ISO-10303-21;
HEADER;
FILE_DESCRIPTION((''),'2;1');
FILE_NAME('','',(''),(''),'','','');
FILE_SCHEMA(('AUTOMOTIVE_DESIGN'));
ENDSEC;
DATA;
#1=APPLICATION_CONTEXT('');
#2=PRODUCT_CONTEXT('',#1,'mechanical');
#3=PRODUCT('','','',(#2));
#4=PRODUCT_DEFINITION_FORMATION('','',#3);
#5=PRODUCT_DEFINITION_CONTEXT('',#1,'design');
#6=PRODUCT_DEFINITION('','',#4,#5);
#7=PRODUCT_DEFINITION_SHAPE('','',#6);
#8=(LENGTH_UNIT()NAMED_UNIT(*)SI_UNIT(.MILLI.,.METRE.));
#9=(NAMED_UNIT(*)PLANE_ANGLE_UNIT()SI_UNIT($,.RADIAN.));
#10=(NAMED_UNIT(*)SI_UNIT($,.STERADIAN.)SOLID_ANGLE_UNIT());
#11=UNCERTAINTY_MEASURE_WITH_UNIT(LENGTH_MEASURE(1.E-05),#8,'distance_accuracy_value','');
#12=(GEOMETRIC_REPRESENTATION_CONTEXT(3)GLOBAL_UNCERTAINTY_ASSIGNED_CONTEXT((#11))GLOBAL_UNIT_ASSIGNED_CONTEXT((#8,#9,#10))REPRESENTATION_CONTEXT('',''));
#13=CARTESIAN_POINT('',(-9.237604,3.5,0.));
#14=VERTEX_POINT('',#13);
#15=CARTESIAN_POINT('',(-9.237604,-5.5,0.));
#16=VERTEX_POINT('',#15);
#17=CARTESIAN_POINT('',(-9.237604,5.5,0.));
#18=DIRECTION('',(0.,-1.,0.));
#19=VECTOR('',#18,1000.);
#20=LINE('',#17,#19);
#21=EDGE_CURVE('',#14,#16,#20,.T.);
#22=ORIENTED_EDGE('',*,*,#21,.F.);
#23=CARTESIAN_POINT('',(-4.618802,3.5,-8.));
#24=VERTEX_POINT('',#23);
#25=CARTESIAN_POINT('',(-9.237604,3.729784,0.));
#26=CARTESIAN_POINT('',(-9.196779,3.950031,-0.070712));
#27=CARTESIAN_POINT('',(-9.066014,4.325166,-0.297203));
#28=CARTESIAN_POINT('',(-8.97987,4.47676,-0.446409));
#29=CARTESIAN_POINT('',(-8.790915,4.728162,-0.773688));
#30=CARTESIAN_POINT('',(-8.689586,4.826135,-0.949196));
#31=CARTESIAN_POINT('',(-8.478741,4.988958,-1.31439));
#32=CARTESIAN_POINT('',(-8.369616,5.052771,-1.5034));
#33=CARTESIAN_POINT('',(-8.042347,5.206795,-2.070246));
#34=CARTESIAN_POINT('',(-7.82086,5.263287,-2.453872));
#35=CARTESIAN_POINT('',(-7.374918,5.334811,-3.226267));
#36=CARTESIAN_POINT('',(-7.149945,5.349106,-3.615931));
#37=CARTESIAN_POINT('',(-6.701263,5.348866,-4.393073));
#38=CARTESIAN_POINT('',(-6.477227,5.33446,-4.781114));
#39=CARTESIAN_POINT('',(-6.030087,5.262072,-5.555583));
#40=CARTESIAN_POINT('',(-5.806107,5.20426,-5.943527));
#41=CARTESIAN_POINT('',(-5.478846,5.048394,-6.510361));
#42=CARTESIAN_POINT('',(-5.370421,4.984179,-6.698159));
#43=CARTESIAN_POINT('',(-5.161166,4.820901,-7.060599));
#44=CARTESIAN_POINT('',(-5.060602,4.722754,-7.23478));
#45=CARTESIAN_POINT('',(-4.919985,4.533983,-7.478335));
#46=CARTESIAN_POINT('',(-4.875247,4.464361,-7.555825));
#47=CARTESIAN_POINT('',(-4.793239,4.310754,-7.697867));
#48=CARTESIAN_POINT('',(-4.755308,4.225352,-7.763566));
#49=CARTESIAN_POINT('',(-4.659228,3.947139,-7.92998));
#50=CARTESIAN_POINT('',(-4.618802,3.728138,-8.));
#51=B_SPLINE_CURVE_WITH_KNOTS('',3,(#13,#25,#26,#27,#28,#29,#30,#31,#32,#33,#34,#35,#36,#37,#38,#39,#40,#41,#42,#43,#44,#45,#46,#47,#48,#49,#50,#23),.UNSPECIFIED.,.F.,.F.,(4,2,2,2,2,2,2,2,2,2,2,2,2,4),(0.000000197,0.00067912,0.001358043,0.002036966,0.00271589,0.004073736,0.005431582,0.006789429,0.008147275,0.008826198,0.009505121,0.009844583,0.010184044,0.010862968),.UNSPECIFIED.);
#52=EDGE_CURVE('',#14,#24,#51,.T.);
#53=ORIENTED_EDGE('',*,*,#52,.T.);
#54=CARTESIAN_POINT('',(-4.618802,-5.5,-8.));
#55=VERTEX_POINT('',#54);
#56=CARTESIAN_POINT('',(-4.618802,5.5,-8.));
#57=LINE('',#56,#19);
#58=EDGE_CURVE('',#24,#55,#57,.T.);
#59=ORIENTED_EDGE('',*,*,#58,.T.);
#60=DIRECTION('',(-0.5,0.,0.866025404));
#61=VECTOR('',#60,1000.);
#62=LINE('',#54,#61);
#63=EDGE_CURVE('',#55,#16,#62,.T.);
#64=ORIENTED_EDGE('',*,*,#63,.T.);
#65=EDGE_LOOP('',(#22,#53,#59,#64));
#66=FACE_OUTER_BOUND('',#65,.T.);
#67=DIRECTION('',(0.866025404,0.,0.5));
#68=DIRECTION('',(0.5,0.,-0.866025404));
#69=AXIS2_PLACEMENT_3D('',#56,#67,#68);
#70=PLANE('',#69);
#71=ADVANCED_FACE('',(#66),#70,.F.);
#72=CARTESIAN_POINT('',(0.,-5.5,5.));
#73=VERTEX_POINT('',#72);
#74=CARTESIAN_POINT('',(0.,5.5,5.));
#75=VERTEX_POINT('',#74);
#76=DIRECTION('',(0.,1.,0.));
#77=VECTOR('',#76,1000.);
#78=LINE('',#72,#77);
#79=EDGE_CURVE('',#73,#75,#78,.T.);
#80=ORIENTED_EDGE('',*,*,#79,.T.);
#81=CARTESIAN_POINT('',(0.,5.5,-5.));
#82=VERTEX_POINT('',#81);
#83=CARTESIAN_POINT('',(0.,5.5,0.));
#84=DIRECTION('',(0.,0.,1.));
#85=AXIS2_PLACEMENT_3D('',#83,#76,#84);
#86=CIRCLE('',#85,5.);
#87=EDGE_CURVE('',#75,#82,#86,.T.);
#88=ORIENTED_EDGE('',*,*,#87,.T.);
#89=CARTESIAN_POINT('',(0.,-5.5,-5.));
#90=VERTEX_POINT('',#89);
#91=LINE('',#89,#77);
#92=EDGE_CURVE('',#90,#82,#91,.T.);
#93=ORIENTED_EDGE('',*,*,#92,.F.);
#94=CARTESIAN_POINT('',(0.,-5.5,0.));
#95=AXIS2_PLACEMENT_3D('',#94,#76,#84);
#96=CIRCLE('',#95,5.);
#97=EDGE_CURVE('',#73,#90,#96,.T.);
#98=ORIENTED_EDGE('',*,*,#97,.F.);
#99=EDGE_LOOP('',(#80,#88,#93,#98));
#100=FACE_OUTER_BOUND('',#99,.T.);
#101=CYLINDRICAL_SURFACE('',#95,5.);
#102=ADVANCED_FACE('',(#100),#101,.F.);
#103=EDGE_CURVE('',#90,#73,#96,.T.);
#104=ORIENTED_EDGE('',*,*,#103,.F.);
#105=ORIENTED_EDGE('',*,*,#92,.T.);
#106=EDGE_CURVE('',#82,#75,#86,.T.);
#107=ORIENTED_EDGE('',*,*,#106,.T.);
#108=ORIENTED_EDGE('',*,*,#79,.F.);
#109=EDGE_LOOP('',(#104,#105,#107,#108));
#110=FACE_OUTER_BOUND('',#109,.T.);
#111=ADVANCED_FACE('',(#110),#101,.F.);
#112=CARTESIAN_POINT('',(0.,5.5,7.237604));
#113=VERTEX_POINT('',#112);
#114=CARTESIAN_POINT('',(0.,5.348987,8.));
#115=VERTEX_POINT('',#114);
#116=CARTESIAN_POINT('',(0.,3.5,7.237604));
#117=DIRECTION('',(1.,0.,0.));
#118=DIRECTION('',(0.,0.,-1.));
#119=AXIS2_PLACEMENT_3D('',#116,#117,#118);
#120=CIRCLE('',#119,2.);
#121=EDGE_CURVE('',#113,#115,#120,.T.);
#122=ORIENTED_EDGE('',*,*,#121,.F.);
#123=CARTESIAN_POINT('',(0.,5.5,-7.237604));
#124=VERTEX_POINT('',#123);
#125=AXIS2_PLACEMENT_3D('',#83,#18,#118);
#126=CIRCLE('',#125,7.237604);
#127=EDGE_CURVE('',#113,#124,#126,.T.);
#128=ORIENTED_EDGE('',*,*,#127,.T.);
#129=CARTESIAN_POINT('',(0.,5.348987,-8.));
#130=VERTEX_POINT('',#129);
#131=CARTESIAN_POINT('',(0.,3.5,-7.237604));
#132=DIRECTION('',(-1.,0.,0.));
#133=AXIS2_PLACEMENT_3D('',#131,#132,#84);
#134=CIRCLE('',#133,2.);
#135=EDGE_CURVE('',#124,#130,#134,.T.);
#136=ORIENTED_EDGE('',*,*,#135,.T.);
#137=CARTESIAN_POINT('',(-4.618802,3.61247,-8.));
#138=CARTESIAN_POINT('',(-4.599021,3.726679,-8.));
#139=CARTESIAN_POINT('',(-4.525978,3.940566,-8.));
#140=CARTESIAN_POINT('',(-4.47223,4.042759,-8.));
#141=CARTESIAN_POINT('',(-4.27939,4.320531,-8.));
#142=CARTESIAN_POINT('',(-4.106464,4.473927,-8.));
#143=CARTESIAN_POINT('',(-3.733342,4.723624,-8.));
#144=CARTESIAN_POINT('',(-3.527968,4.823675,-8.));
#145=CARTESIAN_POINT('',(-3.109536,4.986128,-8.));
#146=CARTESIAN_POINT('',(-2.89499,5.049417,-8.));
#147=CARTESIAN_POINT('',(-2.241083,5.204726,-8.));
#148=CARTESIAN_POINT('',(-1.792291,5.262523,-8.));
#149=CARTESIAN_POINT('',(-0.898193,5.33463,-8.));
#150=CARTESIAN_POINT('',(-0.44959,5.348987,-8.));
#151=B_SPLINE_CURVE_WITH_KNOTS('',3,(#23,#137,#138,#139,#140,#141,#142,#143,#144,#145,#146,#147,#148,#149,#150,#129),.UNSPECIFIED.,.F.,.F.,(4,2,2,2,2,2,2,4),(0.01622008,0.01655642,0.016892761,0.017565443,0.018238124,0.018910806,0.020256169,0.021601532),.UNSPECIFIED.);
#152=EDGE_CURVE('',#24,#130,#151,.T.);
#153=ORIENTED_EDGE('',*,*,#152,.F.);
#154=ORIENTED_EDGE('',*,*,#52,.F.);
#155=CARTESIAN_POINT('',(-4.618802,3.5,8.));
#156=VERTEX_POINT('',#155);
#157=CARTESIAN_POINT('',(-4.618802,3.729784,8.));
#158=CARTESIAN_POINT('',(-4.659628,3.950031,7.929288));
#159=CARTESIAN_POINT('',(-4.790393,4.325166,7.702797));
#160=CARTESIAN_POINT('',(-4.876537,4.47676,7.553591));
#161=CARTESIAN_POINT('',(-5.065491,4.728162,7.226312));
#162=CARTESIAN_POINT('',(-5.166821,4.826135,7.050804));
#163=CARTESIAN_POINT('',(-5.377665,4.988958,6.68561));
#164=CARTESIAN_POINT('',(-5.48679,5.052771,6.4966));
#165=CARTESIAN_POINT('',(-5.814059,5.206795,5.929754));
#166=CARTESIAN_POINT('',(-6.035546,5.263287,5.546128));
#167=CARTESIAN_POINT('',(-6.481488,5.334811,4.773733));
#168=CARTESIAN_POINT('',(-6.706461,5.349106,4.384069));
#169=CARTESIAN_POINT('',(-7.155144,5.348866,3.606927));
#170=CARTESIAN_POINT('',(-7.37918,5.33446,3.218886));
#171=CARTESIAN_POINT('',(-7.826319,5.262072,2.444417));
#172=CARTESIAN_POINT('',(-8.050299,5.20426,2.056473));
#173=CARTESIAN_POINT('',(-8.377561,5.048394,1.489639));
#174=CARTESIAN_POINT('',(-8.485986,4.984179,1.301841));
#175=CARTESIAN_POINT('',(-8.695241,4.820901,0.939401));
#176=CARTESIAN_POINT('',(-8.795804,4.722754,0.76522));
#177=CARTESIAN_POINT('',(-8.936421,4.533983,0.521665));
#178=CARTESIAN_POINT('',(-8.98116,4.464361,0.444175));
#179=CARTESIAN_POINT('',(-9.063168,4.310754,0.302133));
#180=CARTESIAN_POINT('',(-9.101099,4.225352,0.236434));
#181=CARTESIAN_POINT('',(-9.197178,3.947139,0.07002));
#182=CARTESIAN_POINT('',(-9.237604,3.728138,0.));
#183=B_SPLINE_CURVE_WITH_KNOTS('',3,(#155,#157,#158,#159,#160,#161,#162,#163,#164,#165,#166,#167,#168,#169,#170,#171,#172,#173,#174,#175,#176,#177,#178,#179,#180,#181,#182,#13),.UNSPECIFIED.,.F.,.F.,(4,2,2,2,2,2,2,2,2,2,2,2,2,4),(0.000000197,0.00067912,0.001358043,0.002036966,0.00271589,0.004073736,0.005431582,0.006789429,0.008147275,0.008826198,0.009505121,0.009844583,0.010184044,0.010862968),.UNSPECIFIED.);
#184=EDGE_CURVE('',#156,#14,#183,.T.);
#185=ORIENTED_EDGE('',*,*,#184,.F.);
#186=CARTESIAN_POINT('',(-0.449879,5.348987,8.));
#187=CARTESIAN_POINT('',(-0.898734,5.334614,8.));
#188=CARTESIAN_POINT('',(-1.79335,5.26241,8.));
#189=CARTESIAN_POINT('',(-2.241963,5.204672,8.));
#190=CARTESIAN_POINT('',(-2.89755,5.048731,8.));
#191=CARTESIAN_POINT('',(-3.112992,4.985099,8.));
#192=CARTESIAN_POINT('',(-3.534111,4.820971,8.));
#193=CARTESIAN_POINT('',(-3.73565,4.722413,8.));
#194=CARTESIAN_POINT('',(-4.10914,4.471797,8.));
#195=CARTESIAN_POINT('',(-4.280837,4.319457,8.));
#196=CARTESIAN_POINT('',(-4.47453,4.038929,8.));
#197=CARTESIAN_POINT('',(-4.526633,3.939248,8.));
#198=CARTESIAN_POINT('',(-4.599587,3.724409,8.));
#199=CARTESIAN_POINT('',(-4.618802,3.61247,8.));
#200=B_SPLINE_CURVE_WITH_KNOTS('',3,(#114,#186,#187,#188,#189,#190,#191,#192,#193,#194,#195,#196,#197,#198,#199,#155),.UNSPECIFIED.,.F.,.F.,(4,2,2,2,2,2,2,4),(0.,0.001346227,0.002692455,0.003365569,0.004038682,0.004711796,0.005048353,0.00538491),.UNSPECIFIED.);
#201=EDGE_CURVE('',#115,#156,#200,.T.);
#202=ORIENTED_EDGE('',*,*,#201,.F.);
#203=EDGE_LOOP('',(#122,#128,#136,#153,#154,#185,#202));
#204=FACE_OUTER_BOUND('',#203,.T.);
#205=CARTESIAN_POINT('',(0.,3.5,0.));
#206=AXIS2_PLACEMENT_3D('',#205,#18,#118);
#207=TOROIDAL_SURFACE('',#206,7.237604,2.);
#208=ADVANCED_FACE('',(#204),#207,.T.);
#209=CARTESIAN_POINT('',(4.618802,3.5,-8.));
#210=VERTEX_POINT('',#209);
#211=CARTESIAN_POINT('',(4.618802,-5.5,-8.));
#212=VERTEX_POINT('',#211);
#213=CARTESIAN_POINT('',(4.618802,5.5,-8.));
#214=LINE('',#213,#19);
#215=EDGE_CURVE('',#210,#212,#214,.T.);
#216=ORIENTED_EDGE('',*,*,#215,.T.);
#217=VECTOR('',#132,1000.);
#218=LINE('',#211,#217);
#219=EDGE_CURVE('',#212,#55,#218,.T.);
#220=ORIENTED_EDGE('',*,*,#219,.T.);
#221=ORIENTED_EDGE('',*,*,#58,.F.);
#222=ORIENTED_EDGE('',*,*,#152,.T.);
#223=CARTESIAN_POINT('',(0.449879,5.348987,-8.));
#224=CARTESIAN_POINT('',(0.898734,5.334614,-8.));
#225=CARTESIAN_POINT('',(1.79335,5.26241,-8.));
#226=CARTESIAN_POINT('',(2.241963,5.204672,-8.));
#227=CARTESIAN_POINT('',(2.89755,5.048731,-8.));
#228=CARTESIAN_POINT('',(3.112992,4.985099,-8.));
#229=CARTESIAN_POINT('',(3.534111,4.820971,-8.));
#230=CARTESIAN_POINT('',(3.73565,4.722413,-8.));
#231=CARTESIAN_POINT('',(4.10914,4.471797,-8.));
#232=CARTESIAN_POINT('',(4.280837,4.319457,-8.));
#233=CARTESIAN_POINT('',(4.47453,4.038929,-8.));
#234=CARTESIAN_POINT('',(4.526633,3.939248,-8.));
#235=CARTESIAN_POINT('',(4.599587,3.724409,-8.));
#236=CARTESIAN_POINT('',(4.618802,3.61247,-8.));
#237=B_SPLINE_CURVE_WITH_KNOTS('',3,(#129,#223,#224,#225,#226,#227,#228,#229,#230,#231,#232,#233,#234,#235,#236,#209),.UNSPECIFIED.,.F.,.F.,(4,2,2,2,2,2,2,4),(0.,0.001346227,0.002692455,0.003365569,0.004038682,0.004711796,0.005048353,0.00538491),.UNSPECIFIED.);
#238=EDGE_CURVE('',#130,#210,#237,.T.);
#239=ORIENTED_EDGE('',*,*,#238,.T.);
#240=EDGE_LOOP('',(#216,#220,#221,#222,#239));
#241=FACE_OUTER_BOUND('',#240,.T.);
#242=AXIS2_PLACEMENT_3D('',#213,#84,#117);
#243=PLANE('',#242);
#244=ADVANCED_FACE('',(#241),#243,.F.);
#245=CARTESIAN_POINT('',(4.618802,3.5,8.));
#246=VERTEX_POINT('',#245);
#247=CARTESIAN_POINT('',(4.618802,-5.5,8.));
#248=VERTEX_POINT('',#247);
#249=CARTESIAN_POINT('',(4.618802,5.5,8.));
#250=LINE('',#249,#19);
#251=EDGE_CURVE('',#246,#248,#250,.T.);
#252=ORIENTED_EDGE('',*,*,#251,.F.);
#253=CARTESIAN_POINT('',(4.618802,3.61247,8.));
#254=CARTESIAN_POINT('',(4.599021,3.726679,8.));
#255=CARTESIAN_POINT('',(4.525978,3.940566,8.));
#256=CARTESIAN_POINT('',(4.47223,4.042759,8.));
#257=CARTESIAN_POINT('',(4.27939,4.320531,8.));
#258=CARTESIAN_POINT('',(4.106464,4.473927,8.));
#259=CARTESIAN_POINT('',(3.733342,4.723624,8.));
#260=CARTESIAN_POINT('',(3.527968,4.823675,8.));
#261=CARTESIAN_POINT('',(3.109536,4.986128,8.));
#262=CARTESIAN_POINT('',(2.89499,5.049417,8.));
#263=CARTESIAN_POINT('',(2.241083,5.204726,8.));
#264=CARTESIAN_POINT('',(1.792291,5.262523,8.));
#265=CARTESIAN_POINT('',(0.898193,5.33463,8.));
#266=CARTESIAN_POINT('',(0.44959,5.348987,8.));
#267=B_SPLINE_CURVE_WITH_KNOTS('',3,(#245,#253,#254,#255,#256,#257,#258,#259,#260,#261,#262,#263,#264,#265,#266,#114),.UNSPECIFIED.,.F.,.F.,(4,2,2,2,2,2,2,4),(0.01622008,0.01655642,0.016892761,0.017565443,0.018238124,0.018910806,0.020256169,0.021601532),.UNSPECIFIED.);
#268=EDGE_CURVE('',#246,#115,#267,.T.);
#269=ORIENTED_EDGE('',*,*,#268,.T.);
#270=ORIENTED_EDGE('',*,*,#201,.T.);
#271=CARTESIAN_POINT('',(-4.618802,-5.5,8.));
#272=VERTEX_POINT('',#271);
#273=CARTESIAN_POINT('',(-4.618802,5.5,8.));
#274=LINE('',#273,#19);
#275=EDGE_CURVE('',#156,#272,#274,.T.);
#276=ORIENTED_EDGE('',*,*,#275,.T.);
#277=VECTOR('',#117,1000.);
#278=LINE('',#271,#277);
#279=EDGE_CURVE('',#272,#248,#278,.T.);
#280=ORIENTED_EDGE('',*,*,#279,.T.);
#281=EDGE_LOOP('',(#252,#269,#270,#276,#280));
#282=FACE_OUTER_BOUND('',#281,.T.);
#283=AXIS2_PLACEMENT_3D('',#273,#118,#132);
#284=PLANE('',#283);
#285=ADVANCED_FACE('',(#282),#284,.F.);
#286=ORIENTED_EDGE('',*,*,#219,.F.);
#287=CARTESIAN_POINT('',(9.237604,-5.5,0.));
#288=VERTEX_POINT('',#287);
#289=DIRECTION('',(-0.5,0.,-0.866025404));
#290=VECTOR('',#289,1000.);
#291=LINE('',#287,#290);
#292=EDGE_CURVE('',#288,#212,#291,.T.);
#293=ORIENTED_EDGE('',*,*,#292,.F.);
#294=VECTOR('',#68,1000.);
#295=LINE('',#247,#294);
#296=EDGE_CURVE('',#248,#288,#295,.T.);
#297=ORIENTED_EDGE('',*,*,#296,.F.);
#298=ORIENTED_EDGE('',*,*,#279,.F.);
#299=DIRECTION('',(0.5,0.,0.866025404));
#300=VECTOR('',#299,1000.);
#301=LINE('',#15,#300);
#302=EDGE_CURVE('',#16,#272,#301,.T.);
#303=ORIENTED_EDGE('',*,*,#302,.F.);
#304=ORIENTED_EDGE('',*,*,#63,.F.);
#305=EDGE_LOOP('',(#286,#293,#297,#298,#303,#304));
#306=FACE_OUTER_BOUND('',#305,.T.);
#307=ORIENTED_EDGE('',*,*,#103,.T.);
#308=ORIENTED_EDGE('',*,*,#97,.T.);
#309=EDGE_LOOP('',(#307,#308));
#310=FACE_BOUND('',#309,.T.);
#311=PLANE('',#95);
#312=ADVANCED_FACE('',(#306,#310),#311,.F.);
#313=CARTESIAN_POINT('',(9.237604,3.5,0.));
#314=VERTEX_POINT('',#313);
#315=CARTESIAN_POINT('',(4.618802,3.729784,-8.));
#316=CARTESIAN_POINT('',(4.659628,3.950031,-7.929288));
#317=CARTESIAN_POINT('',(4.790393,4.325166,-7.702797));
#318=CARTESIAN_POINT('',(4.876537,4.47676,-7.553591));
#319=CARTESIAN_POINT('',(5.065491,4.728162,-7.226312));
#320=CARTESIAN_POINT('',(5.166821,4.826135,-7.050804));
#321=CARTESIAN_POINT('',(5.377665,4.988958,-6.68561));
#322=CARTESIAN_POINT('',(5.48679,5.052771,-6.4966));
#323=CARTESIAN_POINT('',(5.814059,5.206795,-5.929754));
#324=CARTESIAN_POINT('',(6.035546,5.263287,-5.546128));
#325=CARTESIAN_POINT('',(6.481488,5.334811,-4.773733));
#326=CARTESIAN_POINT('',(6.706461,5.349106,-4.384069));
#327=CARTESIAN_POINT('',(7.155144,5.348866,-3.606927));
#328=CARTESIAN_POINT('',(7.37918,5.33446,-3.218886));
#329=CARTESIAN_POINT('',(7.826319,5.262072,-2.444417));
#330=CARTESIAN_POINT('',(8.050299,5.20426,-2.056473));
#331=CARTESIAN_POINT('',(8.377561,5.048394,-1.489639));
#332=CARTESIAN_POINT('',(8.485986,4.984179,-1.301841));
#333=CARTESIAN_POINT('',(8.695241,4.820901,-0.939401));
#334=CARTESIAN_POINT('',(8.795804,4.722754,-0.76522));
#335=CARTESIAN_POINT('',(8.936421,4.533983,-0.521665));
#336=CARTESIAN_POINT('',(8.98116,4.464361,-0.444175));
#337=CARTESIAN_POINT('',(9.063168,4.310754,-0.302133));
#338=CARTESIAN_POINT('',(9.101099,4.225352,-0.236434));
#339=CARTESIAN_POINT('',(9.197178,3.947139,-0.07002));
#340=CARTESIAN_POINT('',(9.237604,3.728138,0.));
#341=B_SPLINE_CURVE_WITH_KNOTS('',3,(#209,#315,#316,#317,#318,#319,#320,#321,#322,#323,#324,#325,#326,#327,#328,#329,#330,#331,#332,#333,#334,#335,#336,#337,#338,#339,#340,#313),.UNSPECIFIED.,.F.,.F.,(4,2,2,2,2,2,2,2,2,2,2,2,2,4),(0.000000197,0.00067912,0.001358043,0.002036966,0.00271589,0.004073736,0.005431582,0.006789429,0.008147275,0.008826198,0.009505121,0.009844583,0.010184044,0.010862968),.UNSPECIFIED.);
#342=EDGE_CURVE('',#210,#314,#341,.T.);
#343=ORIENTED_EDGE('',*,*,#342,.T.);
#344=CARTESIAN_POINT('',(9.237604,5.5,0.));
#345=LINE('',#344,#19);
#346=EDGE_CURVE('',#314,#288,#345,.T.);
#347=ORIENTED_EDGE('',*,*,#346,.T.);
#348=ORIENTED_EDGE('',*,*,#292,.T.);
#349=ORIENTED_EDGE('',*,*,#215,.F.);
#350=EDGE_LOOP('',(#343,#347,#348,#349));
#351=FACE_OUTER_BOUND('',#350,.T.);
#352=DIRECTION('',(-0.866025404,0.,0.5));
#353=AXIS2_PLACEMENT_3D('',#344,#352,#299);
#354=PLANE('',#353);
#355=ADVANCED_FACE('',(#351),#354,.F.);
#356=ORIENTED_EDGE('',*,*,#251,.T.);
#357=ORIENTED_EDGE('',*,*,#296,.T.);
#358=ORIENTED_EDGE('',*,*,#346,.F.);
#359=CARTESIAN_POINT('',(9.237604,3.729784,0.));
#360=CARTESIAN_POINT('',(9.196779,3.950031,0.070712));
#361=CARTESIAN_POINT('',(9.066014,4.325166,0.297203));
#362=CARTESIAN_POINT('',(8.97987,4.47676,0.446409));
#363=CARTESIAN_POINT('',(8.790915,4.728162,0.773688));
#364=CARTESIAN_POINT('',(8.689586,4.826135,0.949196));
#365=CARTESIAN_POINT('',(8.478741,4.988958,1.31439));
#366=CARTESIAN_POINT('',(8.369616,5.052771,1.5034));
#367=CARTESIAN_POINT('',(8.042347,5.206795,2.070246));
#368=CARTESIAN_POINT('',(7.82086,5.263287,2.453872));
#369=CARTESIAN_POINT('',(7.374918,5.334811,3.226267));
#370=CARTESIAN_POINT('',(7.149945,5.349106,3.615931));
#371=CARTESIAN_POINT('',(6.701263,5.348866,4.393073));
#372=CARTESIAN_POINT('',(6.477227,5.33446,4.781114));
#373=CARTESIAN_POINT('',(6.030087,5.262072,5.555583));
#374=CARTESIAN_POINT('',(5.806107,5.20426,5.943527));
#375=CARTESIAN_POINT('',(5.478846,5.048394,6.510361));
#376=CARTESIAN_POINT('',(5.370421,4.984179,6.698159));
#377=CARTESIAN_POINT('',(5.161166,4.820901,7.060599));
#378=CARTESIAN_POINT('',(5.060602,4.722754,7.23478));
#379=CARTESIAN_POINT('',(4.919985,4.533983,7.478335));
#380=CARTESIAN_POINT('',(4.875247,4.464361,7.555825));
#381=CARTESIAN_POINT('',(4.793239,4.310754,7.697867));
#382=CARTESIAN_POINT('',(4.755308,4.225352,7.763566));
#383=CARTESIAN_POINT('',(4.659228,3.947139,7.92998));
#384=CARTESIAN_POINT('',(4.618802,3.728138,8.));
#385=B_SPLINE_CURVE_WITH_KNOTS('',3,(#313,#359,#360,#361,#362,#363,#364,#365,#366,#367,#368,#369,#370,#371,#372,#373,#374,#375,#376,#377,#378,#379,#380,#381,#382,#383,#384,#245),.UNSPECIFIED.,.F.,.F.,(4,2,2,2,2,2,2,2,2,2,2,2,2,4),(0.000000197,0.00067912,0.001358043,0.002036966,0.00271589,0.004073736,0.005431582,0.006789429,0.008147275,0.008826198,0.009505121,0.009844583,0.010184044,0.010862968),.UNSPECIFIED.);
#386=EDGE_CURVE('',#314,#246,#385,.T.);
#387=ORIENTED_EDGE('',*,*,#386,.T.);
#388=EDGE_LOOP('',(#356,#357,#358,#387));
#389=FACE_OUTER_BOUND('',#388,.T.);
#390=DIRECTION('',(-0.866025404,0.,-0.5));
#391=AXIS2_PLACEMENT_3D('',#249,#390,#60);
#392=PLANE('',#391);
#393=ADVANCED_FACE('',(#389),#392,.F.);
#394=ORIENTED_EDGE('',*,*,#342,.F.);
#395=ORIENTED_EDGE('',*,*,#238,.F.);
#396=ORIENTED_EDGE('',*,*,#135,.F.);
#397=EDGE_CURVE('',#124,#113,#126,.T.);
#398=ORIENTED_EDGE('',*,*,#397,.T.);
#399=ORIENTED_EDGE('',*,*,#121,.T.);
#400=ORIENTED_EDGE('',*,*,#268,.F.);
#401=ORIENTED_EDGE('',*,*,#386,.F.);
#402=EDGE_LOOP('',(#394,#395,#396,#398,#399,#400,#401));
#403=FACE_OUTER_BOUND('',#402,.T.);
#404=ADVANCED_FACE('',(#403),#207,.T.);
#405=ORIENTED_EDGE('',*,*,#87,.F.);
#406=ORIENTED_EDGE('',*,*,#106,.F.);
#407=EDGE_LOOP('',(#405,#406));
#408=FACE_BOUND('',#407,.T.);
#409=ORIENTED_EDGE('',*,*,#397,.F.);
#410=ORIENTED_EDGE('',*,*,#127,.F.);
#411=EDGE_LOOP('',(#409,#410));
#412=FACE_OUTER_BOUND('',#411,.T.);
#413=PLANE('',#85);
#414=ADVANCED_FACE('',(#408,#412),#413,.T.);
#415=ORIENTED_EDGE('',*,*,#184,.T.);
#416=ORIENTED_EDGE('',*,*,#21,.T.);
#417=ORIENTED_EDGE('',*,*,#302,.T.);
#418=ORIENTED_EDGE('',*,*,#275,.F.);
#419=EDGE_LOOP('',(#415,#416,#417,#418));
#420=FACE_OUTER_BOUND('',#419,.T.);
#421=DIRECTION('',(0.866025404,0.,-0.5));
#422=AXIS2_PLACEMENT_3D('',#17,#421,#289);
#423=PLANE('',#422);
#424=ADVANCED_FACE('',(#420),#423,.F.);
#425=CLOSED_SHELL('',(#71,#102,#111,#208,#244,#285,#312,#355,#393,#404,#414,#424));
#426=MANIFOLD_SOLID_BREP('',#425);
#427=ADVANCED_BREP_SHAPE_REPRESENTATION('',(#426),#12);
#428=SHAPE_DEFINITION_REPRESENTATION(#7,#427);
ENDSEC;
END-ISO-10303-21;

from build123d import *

# Parameters (mm, degrees)
HEX_BODY_16AF_X_11_DEPTH = 5.5
BORE_SKETCH_10_R         = 5
BORE_10_THROUGH_DEPTH    = 17.441816779


with BuildPart() as part:
    # Hex Profile 16AF Sketch → Hex Body 16AF x 11 (new, symmetric)
    with BuildSketch(Plane(origin=(0, 0, 0), x_dir=(1, 0, 0), z_dir=(0, 1, 0))):
        Polygon((9.237604307, 0), (4.618802154, 8), (-4.618802154, 8), (-9.237604307, 0), (-4.618802154, -8), (4.618802154, -8), align=None)
    extrude(amount=HEX_BODY_16AF_X_11_DEPTH, both=True)

    # Chamfer Profile Sketch → Face Chamfer 2mm (revolve, cut)
    with BuildSketch(Plane.XY, mode=Mode.PRIVATE) as face_chamfer_2mm_sk:
        with BuildLine():
            Line((9.237604307, 3.5), (9.237604307, -5.5))
            Line((9.237604307, -5.5), (12.102974232, -5.5))
            Line((12.102974232, -5.5), (12.102974232, 7.625857748))
            Line((12.102974232, 7.625857748), (4.618802154, 7.625857748))
            Line((4.618802154, 7.625857748), (4.618802154, 5.5))
            Line((4.618802154, 5.5), (7.237604307, 5.5))
            ThreePointArc((7.237604307, 5.5), (8.651817869, 4.914213562), (9.237604307, 3.5))
        make_face()
    revolve(face_chamfer_2mm_sk.sketch.rotate(Axis((0, 0, 0), (0, 1, 0)), 90), axis=Axis((0, 0, 0), (0, 1, 0)), mode=Mode.SUBTRACT)

    # Bore Sketch Ø10 → Bore Ø10 Through (cut, through all)
    with BuildSketch(Plane(origin=(0, 5.5, 0), x_dir=(1, 0, 0), z_dir=(0, 1, 0))):
        with Locations(Location((0, 0, 0), (0, 0, 270))):
            Circle(BORE_SKETCH_10_R)
    extrude(amount=-BORE_10_THROUGH_DEPTH, mode=Mode.SUBTRACT)


solid = part.part
